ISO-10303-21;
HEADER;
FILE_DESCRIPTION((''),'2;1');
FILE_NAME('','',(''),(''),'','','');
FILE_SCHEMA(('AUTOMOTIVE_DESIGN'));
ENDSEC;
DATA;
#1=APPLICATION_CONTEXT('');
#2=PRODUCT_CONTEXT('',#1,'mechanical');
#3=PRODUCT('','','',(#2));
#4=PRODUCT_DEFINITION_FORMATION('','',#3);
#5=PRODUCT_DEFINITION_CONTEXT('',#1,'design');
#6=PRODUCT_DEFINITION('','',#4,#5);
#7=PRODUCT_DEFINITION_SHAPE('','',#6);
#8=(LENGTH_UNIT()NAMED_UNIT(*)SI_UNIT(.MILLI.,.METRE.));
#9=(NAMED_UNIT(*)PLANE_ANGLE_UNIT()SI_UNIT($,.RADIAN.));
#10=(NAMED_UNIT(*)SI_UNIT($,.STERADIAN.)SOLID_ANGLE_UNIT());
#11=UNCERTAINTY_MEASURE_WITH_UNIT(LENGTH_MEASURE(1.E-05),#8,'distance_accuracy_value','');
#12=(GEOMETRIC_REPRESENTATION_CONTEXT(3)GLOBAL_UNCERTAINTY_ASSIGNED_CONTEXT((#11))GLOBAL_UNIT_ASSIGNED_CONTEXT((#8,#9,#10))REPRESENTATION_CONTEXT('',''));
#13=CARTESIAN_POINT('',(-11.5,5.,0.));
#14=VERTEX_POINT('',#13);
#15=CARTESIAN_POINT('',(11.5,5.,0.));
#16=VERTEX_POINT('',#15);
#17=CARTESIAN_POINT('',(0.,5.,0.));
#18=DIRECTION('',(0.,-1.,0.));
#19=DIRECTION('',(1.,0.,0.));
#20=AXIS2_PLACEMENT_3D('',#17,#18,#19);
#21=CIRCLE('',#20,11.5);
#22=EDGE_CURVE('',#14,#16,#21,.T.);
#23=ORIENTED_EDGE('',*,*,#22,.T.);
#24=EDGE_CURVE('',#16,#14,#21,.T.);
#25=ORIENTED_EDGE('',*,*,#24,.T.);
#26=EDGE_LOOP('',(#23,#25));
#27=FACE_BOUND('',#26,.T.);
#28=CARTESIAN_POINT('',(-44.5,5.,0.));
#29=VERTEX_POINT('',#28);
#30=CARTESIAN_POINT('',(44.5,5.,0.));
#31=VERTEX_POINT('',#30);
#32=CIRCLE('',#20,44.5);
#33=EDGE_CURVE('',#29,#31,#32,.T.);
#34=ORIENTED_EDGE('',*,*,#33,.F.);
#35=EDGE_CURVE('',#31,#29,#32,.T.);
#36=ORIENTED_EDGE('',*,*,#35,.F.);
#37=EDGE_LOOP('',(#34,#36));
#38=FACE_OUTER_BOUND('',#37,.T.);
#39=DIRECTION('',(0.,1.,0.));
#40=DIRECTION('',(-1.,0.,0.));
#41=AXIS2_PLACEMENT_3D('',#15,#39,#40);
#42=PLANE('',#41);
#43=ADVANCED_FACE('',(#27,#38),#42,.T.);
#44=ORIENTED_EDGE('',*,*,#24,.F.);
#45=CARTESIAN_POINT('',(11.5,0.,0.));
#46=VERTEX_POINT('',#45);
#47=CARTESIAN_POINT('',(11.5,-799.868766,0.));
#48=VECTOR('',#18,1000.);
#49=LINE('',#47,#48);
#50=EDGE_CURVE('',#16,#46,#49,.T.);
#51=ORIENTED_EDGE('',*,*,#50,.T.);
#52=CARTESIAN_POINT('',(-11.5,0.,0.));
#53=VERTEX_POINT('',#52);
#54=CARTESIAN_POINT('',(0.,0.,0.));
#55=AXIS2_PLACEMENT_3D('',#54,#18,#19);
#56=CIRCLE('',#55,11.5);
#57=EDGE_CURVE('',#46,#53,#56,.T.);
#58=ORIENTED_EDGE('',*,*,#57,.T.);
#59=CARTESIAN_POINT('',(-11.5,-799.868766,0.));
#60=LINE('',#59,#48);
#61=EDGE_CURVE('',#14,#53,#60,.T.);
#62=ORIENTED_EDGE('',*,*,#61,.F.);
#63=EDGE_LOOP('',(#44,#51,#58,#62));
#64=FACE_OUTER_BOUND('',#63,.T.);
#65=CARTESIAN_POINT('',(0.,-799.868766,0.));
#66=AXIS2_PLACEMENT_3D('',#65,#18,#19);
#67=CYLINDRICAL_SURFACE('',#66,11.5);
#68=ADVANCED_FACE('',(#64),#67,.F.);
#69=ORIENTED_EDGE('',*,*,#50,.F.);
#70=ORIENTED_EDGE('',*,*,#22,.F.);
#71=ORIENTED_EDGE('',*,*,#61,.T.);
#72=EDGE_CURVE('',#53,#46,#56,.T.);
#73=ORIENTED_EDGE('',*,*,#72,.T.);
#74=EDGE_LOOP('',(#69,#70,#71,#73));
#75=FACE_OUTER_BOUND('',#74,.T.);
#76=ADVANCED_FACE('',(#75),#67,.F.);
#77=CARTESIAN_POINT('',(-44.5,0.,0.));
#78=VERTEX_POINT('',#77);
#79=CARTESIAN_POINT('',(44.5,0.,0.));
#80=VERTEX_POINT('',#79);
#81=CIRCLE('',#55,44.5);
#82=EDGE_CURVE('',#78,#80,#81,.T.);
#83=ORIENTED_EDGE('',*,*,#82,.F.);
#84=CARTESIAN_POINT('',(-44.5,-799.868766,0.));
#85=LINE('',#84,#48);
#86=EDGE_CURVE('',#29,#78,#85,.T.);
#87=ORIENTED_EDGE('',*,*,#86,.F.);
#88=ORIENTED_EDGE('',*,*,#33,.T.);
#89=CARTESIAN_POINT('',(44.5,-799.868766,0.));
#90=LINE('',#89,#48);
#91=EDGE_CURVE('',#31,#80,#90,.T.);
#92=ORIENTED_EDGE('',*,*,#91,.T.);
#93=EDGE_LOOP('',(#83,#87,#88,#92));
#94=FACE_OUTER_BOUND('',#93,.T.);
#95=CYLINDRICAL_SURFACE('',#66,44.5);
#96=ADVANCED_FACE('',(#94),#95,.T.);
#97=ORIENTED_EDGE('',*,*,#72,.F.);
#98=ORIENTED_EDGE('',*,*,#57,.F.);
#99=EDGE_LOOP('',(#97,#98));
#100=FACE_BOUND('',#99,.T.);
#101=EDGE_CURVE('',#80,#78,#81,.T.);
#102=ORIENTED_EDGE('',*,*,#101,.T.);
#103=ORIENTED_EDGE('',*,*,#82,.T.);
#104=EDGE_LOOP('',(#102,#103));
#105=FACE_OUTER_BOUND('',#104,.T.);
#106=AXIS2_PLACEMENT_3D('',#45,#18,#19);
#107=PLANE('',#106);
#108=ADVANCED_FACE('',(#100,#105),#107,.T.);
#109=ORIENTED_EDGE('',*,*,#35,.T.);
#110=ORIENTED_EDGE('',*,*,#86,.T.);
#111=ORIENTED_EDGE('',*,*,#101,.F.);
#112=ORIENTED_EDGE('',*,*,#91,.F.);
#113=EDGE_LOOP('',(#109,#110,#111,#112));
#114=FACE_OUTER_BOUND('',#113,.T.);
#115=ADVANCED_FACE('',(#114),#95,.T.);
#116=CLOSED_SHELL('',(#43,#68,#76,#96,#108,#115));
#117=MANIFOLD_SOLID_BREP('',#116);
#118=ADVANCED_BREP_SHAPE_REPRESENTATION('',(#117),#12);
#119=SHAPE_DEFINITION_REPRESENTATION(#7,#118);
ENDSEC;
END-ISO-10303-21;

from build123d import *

# Parameters (mm, degrees)
SKETCH1_W = 33
SKETCH1_H = 5


with BuildPart() as part:
    # Sketch1 → Revolve1 (revolve)
    with BuildSketch(Plane.XY):
        with Locations((28, 2.5)):
            Rectangle(SKETCH1_W, SKETCH1_H)
    revolve(axis=Axis((0, -799.868766404, 0), (0, 1, 0)))


solid = part.part
